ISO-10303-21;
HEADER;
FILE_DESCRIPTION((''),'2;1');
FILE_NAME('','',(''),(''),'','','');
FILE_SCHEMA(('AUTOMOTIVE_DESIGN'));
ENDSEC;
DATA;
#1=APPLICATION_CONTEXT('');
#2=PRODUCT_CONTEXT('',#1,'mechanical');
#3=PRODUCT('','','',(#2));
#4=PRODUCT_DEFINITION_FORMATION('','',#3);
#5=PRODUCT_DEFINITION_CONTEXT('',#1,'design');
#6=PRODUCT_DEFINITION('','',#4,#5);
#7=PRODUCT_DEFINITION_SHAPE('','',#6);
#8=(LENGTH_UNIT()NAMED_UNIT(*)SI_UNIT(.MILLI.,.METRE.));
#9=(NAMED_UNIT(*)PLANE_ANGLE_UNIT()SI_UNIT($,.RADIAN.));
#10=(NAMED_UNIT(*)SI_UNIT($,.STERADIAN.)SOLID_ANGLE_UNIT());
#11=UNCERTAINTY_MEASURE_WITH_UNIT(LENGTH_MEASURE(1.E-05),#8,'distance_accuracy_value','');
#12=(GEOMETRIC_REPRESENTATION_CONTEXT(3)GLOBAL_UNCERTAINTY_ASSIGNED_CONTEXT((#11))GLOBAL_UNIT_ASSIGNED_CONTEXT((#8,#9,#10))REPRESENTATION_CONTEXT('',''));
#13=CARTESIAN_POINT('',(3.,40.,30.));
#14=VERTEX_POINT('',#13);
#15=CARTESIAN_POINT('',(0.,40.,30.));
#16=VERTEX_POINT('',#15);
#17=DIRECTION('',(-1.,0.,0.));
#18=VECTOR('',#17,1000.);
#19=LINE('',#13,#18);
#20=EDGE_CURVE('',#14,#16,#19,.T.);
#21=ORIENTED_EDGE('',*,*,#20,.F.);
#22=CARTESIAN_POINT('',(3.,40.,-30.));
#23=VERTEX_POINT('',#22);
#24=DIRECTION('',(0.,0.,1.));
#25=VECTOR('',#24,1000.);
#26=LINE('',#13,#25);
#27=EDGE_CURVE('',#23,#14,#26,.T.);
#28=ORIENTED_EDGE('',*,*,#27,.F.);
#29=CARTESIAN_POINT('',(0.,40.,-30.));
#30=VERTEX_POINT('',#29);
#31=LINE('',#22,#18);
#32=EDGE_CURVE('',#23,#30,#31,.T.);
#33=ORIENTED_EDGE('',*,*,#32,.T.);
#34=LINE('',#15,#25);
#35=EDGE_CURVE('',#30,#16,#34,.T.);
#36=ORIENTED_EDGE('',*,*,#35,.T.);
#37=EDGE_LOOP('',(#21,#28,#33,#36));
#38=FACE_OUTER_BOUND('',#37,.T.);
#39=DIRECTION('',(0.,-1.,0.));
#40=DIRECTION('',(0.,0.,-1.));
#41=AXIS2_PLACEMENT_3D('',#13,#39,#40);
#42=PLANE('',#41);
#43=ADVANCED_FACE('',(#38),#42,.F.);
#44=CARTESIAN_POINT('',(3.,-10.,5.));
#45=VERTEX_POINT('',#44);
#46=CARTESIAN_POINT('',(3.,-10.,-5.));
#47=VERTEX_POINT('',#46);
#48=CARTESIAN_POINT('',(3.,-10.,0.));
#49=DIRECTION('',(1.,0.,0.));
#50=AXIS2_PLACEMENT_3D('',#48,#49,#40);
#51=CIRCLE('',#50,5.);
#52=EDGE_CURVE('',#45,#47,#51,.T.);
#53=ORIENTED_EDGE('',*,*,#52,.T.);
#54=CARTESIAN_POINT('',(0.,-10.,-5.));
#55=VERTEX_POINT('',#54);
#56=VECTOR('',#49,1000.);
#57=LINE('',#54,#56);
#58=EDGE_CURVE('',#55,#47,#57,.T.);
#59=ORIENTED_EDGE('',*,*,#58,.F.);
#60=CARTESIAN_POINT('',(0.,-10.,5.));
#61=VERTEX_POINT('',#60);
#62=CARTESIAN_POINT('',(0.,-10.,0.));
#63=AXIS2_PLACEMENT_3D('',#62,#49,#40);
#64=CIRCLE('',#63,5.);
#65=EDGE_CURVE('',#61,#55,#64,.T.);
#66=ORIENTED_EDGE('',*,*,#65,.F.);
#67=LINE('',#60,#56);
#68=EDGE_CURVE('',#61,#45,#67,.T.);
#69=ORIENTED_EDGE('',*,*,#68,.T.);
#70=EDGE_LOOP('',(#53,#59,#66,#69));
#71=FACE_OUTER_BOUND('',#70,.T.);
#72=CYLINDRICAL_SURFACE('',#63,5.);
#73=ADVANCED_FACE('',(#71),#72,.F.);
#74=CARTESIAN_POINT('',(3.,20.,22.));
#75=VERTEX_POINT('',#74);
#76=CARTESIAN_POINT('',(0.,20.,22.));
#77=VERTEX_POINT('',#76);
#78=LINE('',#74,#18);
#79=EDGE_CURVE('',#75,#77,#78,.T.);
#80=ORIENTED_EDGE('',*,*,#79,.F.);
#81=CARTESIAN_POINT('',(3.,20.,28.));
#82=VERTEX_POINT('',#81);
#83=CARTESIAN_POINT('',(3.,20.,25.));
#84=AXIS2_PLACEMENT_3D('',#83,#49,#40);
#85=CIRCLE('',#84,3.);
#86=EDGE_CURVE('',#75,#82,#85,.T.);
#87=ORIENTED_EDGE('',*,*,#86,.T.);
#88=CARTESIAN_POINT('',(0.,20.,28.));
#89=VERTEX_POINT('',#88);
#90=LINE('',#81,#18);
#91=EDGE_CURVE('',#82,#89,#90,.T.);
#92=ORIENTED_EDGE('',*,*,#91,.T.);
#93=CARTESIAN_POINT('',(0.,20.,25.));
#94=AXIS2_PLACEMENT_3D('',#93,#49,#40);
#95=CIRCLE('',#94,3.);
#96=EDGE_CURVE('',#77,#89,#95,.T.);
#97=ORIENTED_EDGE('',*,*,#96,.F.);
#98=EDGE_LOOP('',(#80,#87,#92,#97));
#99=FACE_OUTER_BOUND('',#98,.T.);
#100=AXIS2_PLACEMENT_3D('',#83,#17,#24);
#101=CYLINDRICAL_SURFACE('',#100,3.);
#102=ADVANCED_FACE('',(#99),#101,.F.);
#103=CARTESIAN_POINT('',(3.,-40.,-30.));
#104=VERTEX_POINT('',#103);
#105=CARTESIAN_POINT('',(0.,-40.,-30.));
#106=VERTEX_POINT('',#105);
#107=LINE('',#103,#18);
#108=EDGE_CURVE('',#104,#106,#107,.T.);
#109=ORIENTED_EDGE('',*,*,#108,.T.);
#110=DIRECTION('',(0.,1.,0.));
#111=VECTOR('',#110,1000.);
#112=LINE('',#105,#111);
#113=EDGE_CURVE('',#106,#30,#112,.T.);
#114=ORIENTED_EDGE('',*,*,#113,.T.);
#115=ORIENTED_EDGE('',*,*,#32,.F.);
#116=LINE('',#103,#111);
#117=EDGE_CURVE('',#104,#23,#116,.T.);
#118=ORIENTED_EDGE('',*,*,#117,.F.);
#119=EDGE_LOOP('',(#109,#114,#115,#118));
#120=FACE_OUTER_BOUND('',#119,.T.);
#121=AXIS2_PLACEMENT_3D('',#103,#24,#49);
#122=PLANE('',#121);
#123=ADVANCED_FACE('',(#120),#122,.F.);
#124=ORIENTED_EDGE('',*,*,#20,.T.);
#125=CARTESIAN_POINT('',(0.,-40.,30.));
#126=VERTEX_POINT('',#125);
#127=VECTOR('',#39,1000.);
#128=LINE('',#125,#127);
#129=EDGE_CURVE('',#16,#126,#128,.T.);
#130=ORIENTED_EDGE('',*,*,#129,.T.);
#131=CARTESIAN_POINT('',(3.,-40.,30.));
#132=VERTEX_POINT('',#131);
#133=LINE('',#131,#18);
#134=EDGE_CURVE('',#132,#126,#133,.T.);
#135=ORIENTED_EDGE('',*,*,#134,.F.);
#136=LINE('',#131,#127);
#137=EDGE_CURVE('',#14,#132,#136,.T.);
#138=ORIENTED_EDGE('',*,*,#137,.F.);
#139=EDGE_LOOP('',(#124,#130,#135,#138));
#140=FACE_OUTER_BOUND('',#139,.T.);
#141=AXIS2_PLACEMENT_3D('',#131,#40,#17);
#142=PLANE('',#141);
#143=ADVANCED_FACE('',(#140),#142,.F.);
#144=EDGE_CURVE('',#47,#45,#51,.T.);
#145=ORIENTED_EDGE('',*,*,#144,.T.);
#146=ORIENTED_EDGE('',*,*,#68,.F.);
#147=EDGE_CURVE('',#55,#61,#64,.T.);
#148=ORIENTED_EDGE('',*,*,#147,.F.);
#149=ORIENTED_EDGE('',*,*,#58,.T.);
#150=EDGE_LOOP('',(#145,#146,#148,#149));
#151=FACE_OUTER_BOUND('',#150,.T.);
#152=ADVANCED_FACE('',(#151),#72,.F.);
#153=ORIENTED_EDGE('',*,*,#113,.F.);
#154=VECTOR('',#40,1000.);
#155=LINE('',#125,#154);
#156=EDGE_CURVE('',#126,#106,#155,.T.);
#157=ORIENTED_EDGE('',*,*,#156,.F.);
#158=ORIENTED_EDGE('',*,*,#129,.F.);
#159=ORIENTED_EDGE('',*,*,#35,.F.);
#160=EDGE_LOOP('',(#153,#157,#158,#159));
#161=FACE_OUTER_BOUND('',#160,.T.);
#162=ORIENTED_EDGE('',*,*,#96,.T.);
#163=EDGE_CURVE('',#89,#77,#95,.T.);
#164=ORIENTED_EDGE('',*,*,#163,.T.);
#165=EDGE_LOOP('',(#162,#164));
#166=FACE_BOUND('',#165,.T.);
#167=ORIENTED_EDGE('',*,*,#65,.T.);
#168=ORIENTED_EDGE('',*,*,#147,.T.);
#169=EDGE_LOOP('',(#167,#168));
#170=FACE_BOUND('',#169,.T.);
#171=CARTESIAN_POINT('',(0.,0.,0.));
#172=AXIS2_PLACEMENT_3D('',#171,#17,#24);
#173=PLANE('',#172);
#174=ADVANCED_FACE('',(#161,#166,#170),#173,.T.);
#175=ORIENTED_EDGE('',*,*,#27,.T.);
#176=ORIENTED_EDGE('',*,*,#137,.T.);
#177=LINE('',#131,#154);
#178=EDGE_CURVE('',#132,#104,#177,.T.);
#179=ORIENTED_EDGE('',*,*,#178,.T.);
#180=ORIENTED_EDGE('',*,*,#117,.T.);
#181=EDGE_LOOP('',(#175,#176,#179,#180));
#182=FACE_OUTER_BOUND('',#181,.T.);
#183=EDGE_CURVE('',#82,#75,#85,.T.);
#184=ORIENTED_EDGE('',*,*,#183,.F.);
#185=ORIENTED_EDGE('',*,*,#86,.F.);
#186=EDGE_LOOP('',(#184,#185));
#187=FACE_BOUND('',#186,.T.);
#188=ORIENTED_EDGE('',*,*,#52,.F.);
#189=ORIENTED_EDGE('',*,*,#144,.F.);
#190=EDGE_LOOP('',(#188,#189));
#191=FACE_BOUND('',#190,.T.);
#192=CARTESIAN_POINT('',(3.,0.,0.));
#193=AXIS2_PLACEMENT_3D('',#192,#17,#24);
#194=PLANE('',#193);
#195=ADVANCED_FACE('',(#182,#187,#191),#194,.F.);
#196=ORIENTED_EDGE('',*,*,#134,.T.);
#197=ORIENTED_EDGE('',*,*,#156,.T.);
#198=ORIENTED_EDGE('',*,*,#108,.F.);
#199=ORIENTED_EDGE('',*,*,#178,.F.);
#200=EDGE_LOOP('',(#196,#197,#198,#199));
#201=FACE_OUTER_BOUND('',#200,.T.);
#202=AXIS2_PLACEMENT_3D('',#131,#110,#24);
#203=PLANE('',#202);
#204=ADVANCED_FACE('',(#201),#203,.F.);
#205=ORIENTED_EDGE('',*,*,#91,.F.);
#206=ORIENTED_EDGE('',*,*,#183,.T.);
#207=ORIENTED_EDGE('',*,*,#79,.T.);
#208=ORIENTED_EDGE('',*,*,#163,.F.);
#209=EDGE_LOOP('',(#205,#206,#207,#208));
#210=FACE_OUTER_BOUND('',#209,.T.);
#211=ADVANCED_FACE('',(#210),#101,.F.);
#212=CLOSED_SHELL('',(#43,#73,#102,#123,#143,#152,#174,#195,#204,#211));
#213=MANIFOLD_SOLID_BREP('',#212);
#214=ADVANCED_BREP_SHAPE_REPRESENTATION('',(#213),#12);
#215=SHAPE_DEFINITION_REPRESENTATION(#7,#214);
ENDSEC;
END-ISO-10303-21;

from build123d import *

# Parameters (mm, degrees)
SKETCH1_W           = 60
SKETCH1_H           = 80
SKETCH1_R           = 3
BOSS_EXTRUDE1_DEPTH = 3
SKETCH2_R           = 5
CUT_EXTRUDE1_DEPTH  = 3


with BuildPart() as part:
    # Sketch1 → Boss-Extrude1 (new body)
    with BuildSketch(Plane(origin=(0, 0, 0), x_dir=(0, 0, -1), z_dir=(1, 0, 0))):
        Rectangle(SKETCH1_W, SKETCH1_H)
        with Locations((-25, 20)):
            Circle(SKETCH1_R, mode=Mode.SUBTRACT)
        with Locations((0, -10)):
            Circle(SKETCH1_R, mode=Mode.SUBTRACT)
    extrude(amount=BOSS_EXTRUDE1_DEPTH)

    # Sketch2 → Cut-Extrude1 (cut)
    with BuildSketch(Plane(origin=(3, 0, 0), x_dir=(0, 0, -1), z_dir=(1, 0, 0))):
        with Locations((0, -10)):
            Circle(SKETCH2_R)
    extrude(amount=-CUT_EXTRUDE1_DEPTH, mode=Mode.SUBTRACT)


solid = part.part
